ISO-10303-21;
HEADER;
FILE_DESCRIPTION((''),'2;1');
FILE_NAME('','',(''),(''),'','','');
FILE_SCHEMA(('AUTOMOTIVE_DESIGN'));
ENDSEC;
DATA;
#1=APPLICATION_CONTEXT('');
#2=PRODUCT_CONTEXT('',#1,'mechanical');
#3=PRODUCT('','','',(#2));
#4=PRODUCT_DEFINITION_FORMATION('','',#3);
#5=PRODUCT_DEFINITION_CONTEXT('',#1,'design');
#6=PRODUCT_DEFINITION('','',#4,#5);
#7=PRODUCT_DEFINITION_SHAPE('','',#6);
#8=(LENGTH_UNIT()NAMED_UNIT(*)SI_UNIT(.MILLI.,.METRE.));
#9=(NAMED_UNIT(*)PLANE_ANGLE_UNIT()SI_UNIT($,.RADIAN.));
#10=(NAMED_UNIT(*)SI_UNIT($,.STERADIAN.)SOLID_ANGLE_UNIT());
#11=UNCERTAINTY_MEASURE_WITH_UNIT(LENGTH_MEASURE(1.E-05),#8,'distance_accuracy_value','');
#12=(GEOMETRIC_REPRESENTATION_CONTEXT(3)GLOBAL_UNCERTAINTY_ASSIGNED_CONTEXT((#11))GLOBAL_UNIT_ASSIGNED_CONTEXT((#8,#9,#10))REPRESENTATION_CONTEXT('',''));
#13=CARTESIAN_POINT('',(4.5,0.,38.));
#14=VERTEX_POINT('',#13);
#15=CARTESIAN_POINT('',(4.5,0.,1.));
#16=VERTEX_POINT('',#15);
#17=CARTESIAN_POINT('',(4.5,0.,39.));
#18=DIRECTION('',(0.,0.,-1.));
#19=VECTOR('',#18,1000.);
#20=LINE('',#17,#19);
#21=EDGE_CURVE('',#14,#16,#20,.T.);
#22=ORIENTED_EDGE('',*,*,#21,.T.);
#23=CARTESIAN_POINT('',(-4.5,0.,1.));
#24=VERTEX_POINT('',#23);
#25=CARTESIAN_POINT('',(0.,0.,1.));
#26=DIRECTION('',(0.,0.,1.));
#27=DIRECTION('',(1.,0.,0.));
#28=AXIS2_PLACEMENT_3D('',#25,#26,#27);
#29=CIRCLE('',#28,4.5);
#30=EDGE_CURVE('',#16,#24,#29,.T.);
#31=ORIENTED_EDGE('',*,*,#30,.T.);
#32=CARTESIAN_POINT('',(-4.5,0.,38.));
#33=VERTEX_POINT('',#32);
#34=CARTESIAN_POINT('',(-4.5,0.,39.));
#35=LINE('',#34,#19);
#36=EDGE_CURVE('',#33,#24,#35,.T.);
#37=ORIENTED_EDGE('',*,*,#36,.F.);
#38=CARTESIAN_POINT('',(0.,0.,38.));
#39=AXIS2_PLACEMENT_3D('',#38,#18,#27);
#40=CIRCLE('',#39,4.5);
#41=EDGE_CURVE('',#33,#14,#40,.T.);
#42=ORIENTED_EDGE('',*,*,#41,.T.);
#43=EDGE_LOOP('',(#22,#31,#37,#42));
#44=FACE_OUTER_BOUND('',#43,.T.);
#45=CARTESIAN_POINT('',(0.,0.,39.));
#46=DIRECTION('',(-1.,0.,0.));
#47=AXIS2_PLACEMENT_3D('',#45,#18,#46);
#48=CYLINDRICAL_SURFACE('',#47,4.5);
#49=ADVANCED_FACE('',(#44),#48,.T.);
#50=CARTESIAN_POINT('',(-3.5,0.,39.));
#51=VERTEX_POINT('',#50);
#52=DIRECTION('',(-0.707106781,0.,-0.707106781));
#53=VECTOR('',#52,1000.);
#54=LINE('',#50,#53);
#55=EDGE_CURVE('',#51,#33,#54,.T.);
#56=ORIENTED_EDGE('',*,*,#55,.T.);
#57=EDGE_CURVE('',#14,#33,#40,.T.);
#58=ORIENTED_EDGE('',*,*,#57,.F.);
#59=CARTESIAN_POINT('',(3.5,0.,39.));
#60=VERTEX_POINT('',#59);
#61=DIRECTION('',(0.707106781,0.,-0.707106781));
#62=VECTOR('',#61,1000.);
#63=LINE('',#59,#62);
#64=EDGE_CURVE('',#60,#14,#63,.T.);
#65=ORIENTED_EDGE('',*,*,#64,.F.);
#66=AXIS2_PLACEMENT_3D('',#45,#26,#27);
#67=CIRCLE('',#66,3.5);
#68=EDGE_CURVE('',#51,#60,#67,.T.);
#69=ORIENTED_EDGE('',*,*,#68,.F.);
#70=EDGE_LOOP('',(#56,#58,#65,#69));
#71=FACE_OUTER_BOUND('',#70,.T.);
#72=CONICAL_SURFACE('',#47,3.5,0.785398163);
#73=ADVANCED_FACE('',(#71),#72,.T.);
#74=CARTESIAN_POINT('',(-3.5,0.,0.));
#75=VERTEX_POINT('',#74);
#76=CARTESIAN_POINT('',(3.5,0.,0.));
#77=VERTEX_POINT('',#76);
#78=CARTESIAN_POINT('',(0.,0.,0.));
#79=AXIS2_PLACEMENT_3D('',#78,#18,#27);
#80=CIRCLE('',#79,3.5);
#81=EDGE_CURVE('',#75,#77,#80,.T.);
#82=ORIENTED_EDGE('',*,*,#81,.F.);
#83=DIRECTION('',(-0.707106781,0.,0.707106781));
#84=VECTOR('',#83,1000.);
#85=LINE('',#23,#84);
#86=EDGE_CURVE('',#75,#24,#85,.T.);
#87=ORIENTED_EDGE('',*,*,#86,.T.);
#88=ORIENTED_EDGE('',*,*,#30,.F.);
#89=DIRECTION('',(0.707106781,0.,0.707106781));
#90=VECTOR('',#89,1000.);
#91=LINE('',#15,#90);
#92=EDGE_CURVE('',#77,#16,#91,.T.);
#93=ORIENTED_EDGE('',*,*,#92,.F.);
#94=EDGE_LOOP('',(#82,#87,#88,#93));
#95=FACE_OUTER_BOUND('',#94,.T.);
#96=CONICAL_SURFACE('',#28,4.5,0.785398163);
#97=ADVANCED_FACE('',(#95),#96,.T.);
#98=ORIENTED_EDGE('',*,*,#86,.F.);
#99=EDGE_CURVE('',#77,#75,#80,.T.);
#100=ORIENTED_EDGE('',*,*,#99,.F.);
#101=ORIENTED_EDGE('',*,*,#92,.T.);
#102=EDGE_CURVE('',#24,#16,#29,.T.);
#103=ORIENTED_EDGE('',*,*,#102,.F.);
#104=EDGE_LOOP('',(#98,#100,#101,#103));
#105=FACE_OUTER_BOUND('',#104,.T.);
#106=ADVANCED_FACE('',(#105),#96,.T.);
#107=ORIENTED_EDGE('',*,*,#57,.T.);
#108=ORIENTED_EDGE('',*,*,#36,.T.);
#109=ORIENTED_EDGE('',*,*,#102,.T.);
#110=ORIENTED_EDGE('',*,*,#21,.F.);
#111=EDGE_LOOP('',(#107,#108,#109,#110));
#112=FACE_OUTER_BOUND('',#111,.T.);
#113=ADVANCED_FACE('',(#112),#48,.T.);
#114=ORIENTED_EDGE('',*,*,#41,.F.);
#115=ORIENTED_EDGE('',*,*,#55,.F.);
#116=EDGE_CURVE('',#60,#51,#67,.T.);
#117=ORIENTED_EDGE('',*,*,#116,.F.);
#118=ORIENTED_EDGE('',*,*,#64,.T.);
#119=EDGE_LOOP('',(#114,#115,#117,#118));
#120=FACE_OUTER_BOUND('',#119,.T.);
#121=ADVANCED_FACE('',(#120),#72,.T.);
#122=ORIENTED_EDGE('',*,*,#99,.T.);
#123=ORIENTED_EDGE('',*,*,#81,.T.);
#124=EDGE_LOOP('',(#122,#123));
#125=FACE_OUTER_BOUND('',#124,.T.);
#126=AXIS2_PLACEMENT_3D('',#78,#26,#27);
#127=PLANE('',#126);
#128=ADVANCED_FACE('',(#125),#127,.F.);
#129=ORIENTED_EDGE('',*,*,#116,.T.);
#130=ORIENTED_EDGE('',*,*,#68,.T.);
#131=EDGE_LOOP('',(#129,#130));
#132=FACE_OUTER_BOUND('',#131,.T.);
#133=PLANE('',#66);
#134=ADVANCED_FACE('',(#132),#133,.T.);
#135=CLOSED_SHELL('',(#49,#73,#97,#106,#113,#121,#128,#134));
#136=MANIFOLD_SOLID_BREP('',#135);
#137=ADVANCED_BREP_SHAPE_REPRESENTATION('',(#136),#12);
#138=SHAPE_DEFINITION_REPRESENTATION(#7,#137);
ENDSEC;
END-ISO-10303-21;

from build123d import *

# Parameters (mm, degrees)
SKETCH1_R           = 4.5
BOSS_EXTRUDE1_DEPTH = 39
CHAMFER1_SIZE       = 1


with BuildPart() as part:
    # Sketch1 → Boss-Extrude1 (new body)
    with BuildSketch(Plane.XY):
        Circle(SKETCH1_R)
    extrude(amount=BOSS_EXTRUDE1_DEPTH)

    # Chamfer1
    chamfer1_edges = [part.edges().sort_by_distance(p)[0] for p in [
        (-4.5, 0, 0),
        (-4.5, 0, 39),
    ]]
    chamfer(chamfer1_edges, length=CHAMFER1_SIZE)


solid = part.part
